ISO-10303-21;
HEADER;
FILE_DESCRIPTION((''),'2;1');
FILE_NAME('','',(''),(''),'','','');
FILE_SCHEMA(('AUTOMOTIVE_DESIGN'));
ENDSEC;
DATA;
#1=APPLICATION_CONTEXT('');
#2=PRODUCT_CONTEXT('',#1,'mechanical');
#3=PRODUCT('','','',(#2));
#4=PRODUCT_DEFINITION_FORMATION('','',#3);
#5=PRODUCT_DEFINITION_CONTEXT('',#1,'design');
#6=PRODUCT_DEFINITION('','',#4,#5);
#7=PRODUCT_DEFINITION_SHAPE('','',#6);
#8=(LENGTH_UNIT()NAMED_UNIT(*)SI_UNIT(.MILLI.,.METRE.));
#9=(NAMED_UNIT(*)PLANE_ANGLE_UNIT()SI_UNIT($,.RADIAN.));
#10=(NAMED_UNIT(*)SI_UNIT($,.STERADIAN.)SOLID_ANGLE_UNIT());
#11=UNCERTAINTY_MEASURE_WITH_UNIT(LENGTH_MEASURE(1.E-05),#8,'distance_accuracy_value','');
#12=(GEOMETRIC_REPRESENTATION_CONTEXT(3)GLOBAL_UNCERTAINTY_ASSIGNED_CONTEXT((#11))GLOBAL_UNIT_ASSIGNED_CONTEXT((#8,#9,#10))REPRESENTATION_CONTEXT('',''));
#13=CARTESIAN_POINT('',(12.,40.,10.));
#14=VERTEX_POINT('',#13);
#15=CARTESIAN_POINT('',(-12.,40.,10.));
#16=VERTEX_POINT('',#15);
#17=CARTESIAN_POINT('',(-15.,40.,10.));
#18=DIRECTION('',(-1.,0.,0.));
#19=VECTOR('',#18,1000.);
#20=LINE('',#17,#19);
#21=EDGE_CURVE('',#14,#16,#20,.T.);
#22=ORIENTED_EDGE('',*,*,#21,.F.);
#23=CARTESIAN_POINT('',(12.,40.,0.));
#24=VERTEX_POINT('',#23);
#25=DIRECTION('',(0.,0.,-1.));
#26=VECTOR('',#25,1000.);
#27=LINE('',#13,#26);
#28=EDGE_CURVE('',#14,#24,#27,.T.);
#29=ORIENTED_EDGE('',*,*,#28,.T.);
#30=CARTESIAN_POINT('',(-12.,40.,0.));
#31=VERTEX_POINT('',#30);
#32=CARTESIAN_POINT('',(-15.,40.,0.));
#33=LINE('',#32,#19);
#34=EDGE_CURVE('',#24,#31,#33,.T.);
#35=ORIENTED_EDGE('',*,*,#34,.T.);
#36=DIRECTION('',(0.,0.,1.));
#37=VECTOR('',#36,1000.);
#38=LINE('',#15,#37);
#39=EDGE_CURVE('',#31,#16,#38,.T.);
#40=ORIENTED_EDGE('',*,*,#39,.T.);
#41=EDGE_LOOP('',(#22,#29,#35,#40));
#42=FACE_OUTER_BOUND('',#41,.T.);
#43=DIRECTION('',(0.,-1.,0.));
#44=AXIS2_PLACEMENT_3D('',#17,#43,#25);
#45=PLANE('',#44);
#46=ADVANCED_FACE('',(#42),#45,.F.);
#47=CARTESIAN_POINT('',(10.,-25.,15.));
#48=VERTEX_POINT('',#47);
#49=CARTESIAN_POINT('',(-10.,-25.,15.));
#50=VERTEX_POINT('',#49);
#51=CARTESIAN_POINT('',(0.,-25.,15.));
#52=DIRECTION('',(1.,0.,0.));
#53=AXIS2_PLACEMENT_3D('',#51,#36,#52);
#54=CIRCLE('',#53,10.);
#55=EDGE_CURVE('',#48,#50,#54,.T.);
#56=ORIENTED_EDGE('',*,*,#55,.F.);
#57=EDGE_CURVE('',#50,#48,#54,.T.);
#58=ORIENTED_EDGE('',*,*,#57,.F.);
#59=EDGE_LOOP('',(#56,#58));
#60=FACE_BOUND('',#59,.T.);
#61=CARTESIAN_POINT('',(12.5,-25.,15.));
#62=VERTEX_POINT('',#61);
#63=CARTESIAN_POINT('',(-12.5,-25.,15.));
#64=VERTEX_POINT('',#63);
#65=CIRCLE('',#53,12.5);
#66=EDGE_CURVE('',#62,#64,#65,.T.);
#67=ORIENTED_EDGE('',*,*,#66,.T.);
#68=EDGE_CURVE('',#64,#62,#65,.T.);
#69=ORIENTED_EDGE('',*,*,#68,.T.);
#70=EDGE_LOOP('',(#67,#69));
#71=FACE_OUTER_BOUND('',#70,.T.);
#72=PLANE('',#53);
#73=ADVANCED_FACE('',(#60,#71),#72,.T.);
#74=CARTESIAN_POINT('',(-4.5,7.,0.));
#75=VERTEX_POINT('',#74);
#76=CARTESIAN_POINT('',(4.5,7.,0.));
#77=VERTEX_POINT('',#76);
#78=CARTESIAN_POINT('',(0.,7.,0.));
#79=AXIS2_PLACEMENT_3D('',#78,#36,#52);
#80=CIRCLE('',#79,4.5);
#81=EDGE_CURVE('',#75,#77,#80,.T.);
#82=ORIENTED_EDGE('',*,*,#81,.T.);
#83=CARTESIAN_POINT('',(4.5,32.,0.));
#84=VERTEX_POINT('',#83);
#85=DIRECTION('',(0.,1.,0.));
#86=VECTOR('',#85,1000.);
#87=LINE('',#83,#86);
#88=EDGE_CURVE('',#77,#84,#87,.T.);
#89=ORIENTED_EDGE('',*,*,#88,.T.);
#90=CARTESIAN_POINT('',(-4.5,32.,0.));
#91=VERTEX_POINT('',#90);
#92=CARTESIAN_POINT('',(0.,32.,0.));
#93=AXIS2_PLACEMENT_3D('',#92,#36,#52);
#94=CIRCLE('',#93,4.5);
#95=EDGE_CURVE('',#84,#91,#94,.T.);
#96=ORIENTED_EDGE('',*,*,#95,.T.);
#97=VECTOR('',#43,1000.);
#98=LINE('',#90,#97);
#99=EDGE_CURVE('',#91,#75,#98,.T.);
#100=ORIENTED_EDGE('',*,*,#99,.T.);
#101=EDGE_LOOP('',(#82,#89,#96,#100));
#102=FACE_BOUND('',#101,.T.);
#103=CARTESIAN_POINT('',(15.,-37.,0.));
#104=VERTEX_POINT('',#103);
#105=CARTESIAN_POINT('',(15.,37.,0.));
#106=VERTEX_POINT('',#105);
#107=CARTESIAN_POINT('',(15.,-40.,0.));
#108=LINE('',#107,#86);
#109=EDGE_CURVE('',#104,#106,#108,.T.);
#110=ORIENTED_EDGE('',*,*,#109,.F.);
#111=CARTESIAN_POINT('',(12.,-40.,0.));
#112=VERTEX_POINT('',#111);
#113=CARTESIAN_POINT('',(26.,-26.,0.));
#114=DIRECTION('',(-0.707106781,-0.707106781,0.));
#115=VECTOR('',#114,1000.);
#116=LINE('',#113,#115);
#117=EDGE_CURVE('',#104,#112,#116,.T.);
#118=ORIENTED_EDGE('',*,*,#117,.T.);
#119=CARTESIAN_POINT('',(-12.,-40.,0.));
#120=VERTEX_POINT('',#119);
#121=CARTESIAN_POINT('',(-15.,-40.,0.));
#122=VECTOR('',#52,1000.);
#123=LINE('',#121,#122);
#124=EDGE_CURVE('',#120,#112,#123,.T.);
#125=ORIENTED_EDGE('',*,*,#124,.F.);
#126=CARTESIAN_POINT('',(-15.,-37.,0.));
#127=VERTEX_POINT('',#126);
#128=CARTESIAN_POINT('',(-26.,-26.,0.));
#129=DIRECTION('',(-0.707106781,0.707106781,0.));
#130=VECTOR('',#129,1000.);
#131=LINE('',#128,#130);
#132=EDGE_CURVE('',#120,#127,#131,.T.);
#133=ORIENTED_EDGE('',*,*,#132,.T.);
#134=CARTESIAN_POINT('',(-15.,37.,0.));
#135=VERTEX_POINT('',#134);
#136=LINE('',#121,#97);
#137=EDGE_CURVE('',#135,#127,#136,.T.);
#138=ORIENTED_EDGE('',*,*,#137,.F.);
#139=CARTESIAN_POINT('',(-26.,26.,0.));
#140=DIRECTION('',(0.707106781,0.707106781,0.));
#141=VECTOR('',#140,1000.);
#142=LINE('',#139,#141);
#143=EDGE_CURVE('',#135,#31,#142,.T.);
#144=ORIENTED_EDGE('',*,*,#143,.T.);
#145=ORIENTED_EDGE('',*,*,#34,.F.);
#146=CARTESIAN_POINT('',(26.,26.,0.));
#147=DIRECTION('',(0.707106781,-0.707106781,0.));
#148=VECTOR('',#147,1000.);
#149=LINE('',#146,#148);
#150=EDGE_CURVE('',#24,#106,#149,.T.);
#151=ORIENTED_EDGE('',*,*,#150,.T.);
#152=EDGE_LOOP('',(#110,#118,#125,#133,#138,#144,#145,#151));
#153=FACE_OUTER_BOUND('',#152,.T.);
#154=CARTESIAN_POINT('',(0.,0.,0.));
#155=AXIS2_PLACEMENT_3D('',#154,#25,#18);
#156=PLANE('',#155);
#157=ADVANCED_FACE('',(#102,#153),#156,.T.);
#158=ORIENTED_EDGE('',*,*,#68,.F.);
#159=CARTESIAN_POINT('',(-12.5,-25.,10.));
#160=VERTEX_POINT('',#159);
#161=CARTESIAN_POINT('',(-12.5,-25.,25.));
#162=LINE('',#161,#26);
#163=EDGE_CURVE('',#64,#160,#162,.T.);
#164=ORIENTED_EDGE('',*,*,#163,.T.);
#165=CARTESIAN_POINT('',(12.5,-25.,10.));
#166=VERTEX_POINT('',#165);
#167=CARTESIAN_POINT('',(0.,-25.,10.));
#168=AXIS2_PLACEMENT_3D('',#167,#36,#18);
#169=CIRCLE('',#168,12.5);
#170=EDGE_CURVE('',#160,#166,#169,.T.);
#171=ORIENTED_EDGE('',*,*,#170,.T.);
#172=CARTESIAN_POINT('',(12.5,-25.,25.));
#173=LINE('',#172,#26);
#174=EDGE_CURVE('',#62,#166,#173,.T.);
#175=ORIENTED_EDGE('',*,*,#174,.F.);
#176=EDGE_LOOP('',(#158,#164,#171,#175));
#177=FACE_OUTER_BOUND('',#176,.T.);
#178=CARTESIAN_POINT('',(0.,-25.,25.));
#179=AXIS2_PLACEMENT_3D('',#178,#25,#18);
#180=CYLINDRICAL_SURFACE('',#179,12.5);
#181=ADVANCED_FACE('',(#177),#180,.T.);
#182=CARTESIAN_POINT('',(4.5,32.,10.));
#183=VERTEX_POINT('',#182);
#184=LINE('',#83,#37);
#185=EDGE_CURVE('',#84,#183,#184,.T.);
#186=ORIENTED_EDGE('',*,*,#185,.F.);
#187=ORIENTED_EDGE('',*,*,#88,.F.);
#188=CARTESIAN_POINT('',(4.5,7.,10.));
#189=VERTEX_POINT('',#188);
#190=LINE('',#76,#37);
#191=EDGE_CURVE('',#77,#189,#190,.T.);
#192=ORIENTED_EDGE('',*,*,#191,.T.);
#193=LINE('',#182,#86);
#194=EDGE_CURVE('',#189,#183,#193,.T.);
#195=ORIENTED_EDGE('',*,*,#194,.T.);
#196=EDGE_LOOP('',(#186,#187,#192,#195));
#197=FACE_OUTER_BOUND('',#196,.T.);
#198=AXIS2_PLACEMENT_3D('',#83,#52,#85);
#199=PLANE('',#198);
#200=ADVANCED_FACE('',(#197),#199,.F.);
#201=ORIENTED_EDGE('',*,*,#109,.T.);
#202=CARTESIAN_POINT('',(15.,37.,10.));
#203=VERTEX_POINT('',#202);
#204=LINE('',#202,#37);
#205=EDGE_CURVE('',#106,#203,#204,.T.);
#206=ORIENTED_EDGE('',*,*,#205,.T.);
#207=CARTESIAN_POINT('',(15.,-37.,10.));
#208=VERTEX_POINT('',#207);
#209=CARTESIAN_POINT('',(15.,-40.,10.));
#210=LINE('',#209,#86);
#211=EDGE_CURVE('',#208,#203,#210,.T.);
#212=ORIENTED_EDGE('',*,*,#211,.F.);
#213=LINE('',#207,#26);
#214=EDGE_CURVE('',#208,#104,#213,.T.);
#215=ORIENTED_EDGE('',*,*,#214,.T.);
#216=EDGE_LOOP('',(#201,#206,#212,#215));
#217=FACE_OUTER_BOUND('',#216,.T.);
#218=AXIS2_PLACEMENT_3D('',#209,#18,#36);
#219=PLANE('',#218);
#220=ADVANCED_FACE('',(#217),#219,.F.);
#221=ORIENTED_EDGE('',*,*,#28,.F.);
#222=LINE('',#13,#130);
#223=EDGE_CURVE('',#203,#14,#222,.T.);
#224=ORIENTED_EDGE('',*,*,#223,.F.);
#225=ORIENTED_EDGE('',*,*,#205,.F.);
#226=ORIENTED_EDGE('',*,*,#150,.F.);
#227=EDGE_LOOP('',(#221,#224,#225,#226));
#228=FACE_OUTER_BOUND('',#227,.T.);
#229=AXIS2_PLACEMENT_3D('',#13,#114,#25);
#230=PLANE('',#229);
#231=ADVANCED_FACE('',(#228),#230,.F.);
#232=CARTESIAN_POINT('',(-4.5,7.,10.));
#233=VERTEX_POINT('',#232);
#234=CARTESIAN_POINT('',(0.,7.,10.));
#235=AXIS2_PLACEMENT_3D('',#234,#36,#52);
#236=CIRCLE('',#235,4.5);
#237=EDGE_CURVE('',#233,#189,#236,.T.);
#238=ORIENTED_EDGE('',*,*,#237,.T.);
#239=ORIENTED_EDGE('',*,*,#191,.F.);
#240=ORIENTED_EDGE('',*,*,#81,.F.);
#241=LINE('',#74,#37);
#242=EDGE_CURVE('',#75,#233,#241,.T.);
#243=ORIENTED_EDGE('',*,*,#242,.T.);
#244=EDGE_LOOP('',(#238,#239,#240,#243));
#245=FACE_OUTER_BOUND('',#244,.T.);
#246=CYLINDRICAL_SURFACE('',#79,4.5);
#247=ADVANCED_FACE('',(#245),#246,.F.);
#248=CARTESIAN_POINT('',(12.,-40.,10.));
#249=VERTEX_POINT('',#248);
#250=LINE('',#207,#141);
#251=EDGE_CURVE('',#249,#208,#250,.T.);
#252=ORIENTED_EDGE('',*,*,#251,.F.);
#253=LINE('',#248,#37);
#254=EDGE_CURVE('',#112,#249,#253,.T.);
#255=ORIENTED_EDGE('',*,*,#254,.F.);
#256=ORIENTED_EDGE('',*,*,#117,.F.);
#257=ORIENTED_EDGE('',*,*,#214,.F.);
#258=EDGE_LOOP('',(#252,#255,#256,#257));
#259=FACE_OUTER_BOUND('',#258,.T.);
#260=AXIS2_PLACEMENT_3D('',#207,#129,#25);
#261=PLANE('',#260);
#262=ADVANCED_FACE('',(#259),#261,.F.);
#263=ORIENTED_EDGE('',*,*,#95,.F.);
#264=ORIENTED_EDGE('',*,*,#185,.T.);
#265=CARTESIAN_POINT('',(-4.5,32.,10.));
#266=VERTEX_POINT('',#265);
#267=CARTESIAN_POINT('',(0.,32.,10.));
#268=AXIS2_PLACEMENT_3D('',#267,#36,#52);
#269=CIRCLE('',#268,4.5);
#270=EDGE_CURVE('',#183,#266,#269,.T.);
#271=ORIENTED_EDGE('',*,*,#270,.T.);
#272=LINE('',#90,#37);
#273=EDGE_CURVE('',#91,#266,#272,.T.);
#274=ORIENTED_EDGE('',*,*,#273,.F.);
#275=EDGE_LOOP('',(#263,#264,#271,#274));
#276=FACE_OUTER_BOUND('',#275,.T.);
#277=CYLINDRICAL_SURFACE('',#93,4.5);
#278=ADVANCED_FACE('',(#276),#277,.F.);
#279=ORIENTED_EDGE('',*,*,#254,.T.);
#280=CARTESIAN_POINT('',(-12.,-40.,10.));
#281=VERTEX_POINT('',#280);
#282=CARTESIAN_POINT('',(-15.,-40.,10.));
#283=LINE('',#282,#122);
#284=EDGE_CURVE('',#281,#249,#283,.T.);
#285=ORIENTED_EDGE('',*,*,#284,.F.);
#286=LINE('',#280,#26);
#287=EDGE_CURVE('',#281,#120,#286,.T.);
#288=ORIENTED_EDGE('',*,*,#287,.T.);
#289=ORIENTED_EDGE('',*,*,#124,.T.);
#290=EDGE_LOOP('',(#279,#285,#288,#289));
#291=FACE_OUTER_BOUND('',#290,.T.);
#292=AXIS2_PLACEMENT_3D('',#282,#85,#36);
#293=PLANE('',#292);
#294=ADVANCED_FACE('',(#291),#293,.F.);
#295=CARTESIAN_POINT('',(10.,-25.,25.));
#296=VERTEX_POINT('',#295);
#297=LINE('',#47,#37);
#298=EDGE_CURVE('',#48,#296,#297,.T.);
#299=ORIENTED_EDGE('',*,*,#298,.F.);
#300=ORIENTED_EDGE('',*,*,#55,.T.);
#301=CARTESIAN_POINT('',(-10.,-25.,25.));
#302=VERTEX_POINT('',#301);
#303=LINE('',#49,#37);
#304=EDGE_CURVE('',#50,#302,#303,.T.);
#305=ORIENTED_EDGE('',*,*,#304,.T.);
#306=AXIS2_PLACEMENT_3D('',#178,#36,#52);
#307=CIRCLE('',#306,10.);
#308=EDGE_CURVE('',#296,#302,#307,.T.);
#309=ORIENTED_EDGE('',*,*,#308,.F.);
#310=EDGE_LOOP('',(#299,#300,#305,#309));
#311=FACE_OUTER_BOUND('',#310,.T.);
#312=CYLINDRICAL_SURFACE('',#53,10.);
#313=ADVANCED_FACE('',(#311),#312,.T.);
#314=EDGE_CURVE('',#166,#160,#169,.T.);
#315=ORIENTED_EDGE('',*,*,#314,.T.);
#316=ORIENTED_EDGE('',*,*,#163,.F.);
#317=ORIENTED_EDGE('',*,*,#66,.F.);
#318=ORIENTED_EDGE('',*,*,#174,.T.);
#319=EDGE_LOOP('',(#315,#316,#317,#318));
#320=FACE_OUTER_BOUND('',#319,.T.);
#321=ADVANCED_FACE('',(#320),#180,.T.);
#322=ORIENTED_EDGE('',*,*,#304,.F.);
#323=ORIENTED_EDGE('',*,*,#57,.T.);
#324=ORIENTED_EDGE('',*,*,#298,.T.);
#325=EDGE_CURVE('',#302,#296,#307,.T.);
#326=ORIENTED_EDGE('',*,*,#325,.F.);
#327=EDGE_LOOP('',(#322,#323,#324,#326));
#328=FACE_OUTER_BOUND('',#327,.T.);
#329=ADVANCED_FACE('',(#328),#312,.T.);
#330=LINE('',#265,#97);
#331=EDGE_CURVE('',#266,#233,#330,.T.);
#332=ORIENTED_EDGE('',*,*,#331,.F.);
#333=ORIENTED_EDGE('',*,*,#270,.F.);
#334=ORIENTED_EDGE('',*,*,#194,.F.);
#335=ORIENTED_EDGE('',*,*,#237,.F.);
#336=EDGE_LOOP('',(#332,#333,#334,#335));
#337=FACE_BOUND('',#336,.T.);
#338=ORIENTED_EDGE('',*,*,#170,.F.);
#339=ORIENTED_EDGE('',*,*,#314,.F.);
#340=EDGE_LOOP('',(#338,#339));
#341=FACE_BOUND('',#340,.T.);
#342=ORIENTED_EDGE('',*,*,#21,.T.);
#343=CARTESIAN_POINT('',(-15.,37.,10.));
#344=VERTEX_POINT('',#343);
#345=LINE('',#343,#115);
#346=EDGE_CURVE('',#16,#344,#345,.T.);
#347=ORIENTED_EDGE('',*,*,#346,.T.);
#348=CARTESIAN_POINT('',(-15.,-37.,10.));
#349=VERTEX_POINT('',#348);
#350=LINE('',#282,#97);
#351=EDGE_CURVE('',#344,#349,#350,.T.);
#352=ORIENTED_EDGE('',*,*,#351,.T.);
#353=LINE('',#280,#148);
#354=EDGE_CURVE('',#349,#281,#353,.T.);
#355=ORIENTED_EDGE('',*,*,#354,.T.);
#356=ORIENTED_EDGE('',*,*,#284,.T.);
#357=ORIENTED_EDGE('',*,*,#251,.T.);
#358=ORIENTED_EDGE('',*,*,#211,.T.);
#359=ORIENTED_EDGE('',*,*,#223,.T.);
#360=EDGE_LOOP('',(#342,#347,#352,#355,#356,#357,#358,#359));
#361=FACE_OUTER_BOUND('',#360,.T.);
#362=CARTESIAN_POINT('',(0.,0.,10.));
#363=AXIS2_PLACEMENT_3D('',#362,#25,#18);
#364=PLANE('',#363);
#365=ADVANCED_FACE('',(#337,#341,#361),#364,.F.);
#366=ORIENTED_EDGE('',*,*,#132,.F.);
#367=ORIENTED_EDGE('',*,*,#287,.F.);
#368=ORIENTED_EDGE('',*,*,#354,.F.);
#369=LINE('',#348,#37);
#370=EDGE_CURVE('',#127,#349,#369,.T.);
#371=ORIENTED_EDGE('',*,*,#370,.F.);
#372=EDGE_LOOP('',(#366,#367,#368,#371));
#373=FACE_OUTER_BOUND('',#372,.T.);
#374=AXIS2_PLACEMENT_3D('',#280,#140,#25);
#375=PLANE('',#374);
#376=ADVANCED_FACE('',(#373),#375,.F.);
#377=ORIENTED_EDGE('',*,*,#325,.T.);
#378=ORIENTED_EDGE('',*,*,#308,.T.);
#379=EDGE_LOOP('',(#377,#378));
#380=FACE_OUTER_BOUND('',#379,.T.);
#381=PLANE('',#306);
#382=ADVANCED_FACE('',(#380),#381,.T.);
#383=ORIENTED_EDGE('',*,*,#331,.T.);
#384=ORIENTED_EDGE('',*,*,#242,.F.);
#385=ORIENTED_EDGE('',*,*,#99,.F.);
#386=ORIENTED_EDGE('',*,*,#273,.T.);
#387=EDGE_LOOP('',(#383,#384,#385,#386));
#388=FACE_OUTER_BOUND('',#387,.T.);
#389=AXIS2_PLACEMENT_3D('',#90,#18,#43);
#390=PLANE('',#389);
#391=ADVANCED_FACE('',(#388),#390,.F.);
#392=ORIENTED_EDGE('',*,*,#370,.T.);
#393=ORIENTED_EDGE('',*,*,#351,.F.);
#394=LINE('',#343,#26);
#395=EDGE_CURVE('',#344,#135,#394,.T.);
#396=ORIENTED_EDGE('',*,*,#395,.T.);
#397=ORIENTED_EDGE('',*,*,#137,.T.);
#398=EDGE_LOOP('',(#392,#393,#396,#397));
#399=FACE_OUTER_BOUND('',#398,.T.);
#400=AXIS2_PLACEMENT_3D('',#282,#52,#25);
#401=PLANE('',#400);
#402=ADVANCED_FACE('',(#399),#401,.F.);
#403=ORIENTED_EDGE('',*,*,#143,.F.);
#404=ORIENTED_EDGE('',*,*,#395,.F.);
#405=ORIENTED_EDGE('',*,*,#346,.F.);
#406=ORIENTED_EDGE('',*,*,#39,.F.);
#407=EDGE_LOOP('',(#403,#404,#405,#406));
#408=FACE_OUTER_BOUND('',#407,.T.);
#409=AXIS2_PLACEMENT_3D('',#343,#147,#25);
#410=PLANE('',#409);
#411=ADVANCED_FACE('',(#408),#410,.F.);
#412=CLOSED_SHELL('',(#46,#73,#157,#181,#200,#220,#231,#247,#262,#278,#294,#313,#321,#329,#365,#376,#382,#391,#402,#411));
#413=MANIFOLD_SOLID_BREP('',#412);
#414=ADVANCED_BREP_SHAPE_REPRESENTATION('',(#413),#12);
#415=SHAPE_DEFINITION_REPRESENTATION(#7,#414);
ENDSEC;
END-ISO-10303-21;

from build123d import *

# Parameters (mm, degrees)
SKETCH_1_W          = 30
SKETCH_1_H          = 80
EXTRUDE_1_DEPTH     = 10
SKETCH_2_R          = 12.5
EXTRUDE_2_DEPTH     = 15
CUT_EXTRUDE_START   = -10
SKETCH_3_R          = 12.5
SKETCH_3_R_2        = 10
CUT_EXTRUDE_1_DEPTH = 10
CUT_EXTRUDE_2_DEPTH = 46.276925691
CHAMFER_1_SIZE      = 3


with BuildPart() as part:
    # 草图1 → 凸台-拉伸1 (new body)
    with BuildSketch(Plane.XY):
        Rectangle(SKETCH_1_W, SKETCH_1_H)
    extrude(amount=EXTRUDE_1_DEPTH)

    # 草图2 → 凸台-拉伸2 (add)
    with BuildSketch(Plane.XY.offset(10)):
        with Locations(Location((0, -25, 0), (0, 0, 180))):
            Circle(SKETCH_2_R)
    extrude(amount=EXTRUDE_2_DEPTH)

    # 草图3 → 切除-拉伸1 (cut)
    with BuildSketch(Plane.XY.offset(25).offset(CUT_EXTRUDE_START)):
        with Locations(Location((0, -25, 0), (0, 0, 180))):
            Circle(SKETCH_3_R)
        with Locations((0, -25)):
            Circle(SKETCH_3_R_2, mode=Mode.SUBTRACT)
    extrude(amount=CUT_EXTRUDE_1_DEPTH, mode=Mode.SUBTRACT)

    # 草图4 → 切除-拉伸2 (cut, through all)
    with BuildSketch(Plane.XY.offset(10)):
        with BuildLine():
            Line((4.5, 32), (4.5, 7))
            ThreePointArc((4.5, 7), (0, 2.5), (-4.5, 7))
            Line((-4.5, 7), (-4.5, 32))
            ThreePointArc((-4.5, 32), (0, 36.5), (4.5, 32))
        make_face()
    extrude(amount=-CUT_EXTRUDE_2_DEPTH, mode=Mode.SUBTRACT)

    # 倒角1
    chamfer_1_edges = [part.edges().sort_by_distance(p)[0] for p in [
        (15, -40, 5),
        (-15, -40, 5),
        (-15, 40, 5),
        (15, 40, 5),
    ]]
    chamfer(chamfer_1_edges, length=CHAMFER_1_SIZE)


solid = part.part
